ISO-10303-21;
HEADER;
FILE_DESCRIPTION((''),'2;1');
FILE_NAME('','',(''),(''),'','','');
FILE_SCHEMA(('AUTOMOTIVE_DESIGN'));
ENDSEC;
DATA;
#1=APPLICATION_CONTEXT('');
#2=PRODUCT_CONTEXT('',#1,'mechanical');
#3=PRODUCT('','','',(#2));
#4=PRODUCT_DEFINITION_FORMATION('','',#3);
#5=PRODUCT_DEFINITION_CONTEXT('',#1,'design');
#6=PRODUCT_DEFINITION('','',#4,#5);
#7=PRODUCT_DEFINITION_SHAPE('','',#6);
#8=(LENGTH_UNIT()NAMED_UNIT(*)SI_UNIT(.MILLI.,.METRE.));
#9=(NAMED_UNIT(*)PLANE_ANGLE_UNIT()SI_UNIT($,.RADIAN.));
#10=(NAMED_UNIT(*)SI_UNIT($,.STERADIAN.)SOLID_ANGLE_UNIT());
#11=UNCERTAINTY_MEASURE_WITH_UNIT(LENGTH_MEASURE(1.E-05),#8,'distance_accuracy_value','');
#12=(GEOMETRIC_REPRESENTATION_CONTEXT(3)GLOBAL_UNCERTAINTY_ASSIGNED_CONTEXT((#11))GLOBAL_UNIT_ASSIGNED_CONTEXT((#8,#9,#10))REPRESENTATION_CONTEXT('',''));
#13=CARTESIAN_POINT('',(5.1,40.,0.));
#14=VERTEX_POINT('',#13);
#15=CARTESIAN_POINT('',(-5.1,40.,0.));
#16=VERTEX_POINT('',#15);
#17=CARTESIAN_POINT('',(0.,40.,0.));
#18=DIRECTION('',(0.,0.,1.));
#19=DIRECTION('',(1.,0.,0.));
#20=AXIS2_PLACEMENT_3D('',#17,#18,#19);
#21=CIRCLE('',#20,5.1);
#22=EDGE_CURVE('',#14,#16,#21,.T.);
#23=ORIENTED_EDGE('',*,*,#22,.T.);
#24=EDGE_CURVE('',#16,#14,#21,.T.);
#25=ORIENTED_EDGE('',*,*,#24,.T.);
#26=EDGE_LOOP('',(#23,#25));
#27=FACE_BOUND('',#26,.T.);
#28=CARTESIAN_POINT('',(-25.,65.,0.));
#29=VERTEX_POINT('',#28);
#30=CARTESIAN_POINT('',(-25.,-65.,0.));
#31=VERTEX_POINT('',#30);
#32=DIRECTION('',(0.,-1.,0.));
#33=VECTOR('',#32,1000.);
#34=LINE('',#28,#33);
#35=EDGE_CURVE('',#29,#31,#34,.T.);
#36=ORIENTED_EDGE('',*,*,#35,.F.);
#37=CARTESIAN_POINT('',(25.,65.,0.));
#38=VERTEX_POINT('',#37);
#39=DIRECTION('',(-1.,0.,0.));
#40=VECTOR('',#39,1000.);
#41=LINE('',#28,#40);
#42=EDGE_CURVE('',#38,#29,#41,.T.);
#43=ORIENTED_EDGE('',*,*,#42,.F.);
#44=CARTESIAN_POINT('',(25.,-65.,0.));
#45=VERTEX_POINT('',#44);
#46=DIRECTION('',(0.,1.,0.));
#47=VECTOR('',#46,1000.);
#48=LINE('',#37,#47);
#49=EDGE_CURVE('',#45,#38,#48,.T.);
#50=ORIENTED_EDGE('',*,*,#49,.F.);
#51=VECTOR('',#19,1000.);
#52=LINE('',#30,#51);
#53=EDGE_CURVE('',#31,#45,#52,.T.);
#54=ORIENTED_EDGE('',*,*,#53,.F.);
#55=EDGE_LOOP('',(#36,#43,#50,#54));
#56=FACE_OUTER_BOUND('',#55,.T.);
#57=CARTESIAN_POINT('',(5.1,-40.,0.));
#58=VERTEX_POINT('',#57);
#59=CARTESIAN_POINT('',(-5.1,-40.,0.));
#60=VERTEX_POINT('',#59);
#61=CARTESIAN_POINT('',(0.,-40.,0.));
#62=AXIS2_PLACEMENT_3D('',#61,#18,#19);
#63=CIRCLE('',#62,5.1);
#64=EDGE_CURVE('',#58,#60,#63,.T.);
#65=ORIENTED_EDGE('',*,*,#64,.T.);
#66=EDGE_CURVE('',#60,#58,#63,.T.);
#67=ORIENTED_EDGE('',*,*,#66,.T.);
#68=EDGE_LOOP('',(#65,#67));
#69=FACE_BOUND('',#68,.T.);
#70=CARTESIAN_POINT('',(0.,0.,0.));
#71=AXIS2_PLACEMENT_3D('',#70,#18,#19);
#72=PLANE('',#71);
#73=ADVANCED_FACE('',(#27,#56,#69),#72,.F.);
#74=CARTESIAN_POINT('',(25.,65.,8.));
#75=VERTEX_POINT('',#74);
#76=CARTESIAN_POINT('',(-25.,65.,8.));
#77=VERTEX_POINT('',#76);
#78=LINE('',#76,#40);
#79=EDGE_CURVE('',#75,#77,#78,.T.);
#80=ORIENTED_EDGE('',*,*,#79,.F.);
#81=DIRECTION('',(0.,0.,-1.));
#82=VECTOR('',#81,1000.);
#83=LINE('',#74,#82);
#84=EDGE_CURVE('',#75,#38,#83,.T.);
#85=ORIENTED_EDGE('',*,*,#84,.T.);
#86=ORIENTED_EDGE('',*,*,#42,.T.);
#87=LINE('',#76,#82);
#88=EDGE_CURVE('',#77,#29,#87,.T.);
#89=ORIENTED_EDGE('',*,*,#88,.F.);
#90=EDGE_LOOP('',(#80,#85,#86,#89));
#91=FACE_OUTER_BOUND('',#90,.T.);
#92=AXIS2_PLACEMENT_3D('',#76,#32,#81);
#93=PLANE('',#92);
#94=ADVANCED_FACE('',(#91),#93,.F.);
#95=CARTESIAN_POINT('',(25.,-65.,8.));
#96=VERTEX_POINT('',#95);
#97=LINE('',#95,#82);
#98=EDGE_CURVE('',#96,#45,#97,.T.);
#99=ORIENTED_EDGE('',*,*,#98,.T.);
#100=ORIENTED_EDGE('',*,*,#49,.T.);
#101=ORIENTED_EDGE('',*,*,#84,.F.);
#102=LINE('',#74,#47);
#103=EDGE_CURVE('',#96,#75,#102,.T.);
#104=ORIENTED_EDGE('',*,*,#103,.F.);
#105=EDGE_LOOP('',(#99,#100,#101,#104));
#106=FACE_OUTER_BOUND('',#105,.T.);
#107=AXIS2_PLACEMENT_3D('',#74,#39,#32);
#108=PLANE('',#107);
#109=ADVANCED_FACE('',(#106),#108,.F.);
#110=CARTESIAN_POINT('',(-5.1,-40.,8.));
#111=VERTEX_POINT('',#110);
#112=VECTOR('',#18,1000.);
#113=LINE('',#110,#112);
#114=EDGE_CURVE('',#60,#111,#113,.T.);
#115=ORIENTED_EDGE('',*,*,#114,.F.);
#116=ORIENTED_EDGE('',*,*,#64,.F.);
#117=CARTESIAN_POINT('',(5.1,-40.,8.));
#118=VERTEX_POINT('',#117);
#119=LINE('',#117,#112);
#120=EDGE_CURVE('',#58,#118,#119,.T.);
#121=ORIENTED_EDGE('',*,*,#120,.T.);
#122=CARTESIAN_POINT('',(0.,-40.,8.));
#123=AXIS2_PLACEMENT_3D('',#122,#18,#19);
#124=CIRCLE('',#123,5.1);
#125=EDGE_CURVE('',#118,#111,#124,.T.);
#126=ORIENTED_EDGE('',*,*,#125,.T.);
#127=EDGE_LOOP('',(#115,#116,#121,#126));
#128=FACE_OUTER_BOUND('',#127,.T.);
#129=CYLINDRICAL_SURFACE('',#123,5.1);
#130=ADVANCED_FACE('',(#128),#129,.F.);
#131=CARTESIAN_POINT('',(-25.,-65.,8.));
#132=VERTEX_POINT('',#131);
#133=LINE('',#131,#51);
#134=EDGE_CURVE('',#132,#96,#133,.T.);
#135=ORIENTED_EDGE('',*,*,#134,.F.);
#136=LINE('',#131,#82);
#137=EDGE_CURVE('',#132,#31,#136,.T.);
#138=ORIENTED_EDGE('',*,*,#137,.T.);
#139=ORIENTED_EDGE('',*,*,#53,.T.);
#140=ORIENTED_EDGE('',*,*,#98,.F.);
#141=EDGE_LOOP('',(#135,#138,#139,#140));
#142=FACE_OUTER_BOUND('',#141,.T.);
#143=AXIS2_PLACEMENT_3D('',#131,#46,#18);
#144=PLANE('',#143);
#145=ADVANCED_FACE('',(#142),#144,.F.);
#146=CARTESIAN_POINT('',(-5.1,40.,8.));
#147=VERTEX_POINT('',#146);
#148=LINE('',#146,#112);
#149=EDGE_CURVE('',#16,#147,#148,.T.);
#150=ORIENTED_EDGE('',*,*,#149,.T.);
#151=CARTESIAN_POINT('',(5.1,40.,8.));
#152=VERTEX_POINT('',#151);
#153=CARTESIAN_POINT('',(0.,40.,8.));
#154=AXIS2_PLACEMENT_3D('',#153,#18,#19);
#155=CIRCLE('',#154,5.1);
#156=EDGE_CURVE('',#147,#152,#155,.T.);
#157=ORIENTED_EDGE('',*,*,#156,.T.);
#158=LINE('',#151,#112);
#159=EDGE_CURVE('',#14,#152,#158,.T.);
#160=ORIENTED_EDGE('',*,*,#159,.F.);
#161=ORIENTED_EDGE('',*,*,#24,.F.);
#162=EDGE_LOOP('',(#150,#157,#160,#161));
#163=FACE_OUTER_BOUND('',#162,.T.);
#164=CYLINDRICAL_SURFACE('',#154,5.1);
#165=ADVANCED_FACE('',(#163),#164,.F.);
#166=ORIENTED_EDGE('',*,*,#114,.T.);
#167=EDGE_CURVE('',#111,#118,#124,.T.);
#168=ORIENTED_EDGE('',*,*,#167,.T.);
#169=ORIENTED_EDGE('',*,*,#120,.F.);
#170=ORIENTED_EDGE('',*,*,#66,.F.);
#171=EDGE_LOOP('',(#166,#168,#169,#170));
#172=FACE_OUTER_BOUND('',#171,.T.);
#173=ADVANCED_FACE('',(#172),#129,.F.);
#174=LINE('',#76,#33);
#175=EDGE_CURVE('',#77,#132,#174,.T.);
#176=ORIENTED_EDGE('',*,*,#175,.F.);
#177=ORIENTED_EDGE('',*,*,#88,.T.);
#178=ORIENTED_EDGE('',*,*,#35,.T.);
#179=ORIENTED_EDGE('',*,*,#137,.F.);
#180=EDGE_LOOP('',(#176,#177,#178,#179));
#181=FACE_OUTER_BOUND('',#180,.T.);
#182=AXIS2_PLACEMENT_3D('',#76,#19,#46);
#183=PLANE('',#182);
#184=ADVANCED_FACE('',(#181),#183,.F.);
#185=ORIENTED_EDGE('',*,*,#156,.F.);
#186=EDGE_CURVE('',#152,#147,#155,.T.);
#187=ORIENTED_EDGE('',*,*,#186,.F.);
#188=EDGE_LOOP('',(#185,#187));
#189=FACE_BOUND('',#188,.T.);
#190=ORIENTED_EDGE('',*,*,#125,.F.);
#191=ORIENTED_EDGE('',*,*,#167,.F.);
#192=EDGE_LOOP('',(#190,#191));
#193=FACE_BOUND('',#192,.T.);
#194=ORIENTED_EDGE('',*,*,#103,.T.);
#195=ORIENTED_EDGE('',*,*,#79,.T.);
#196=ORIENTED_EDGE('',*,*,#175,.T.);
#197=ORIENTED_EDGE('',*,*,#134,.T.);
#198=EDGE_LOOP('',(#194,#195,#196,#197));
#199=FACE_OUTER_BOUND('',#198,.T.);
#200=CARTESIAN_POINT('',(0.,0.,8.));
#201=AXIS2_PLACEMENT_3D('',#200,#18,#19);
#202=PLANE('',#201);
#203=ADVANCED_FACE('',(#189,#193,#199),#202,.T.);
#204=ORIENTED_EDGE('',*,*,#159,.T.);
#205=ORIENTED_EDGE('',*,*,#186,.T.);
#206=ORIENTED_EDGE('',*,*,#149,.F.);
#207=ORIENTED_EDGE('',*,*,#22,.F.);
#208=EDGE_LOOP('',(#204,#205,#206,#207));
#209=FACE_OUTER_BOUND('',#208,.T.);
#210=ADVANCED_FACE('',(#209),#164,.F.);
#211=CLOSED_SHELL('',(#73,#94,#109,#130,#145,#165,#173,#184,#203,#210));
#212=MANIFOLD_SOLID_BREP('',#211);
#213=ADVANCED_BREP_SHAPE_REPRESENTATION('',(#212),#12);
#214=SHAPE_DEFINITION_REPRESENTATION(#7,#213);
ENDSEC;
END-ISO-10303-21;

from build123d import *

# Parameters (mm, degrees)
SKETCH1_W              = 50
SKETCH1_H              = 130
BOSS_EXTRUDE1_DEPTH    = 8
M12_TAPPED_HOLE1_D     = 10.2
M12_TAPPED_HOLE1_DEPTH = 29.25
M12_TAPPED_HOLE1_TIP   = 3.064389157


with BuildPart() as part:
    # Sketch1 → Boss-Extrude1 (new body)
    with BuildSketch(Plane.XY):
        Rectangle(SKETCH1_W, SKETCH1_H)
    extrude(amount=BOSS_EXTRUDE1_DEPTH)

    # M12 Tapped Hole1
    with Locations(Plane.XY.offset(8)):
        with Locations((0, 40), (0, -40)):
            Hole(M12_TAPPED_HOLE1_D / 2, depth=M12_TAPPED_HOLE1_DEPTH)
            with Locations((0, 0, -(M12_TAPPED_HOLE1_DEPTH + M12_TAPPED_HOLE1_TIP / 2))):  # 118° drill point
                Cone(0, M12_TAPPED_HOLE1_D / 2, M12_TAPPED_HOLE1_TIP, mode=Mode.SUBTRACT)


solid = part.part
